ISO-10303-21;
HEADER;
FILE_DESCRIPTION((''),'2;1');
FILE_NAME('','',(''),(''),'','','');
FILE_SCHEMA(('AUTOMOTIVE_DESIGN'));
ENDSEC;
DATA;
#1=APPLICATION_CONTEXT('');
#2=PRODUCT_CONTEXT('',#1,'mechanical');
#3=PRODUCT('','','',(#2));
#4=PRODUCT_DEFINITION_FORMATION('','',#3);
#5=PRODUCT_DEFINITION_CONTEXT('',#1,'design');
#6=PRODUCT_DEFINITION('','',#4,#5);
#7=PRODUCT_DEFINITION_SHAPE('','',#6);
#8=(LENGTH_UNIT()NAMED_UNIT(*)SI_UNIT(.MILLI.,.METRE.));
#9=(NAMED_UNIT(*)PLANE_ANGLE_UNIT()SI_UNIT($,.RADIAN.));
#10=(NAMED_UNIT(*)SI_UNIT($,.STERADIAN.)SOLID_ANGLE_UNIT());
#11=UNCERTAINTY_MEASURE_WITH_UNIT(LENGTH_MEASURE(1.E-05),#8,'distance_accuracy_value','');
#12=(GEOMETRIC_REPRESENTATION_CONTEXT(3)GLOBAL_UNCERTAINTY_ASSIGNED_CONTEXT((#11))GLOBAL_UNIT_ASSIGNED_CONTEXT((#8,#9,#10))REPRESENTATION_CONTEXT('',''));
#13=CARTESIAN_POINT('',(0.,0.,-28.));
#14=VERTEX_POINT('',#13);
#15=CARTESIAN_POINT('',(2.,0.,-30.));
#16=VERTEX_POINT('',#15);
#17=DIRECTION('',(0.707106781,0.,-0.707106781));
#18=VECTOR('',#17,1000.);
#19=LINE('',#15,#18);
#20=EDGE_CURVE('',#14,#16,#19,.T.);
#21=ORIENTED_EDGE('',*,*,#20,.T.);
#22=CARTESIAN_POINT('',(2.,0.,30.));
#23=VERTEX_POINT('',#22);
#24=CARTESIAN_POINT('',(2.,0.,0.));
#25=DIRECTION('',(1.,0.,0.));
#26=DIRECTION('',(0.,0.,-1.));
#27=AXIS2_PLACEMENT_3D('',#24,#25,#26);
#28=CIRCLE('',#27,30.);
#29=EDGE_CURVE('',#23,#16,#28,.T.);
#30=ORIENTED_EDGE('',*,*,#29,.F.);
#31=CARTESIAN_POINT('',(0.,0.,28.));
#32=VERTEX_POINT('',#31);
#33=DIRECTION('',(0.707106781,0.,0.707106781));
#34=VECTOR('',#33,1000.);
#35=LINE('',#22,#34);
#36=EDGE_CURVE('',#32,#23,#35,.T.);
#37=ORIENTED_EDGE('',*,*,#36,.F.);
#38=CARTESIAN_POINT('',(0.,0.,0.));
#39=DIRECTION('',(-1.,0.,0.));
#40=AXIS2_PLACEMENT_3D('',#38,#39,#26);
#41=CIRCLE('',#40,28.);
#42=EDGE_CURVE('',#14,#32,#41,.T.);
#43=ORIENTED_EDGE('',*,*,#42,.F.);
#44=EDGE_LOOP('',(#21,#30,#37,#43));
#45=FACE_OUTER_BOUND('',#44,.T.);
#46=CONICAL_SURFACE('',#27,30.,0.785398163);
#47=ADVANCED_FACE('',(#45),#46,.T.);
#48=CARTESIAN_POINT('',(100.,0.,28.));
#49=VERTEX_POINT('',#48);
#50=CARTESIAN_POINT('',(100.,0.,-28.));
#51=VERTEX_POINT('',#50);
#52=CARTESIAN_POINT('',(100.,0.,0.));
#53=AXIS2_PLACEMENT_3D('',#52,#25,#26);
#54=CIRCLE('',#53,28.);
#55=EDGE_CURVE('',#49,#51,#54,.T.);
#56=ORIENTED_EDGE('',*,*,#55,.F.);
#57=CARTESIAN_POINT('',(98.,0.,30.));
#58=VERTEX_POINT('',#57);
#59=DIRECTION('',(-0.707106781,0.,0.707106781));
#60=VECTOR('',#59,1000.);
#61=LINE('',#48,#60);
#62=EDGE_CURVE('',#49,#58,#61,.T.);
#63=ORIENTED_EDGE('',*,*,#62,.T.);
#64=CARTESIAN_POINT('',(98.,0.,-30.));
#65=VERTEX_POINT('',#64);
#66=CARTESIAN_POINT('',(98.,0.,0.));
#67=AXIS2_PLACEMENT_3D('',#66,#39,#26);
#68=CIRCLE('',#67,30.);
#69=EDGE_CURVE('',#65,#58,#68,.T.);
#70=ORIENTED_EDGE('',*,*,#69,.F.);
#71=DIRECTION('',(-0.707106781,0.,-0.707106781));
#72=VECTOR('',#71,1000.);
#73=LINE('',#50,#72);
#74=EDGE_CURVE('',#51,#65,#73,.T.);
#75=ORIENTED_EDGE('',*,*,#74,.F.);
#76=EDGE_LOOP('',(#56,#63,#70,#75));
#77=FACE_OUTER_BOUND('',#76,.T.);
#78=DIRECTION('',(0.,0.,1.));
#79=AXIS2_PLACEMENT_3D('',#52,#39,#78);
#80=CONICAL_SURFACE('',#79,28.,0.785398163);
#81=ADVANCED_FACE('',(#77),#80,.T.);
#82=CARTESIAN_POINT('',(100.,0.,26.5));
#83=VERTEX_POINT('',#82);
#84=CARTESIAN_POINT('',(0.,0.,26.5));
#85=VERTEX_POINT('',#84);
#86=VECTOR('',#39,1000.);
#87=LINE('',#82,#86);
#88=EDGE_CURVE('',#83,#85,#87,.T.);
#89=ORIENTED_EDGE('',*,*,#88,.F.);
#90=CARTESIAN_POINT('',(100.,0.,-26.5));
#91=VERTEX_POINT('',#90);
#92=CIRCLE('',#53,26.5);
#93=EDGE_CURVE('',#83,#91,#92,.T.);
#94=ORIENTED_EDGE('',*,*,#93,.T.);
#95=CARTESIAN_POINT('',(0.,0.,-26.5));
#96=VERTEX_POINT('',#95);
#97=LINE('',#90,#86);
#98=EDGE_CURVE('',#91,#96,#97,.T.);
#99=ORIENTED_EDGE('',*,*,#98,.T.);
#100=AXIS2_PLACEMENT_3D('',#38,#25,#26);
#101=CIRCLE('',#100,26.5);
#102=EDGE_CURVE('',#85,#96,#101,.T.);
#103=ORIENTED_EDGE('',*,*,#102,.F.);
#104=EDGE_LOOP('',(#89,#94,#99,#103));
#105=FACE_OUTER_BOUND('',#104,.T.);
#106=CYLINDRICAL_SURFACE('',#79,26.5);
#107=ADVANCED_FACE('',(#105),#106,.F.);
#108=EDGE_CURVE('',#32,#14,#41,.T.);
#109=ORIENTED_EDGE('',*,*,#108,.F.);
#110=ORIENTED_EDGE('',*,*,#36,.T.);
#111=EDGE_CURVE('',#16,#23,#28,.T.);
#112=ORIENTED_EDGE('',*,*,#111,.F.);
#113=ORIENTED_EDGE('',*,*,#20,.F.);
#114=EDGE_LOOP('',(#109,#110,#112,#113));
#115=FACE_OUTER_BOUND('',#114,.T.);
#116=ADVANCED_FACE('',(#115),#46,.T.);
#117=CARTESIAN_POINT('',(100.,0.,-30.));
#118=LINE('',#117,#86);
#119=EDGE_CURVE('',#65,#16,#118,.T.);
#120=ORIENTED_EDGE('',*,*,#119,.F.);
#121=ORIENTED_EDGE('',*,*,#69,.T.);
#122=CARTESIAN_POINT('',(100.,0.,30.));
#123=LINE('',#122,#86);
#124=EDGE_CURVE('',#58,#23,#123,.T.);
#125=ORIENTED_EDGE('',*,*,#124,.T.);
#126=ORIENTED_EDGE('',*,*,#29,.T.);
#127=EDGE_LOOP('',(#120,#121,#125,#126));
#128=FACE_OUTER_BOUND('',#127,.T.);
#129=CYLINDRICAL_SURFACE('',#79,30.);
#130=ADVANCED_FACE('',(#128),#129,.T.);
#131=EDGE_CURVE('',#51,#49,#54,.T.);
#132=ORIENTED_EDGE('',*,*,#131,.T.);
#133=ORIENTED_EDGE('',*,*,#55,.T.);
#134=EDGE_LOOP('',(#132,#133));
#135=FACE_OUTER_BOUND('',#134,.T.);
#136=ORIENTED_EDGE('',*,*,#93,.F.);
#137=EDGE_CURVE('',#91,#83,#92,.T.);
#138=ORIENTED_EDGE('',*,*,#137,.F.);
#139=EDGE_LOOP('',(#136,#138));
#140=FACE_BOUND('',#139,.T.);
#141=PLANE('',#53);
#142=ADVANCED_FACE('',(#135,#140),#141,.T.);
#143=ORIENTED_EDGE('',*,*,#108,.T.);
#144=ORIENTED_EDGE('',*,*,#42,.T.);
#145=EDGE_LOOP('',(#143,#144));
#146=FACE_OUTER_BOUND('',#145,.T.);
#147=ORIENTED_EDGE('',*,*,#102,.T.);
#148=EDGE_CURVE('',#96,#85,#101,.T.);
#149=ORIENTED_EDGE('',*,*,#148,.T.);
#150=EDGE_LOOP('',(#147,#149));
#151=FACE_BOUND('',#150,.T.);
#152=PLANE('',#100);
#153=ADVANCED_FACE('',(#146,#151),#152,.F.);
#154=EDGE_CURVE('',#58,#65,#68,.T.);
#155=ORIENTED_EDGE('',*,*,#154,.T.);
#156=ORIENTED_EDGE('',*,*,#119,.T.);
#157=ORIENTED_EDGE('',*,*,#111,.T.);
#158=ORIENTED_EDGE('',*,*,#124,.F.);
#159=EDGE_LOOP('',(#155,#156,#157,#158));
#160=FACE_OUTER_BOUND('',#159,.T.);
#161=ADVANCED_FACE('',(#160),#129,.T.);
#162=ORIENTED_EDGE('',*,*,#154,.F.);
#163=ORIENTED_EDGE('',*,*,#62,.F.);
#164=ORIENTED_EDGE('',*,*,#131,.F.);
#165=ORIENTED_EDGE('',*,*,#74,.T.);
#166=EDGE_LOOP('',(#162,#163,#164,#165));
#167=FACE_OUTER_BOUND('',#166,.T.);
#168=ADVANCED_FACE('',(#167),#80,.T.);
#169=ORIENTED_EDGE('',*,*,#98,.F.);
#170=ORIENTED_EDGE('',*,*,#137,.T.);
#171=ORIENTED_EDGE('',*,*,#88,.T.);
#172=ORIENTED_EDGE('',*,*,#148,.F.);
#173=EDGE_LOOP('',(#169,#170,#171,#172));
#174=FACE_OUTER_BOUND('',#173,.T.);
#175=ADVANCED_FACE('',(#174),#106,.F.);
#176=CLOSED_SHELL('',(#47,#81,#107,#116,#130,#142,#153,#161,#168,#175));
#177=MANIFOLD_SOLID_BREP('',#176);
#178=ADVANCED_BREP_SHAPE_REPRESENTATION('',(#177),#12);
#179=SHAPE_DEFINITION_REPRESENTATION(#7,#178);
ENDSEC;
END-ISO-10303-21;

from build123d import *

# Parameters (mm, degrees)
SKETCH_1_R      = 30
SKETCH_1_R_2    = 26.5
EXTRUDE_1_DEPTH = 100
CHAMFER_1_SIZE  = 2


with BuildPart() as part:
    # 草图1 → 拉伸-薄壁1 (new body)
    with BuildSketch(Plane(origin=(0, 0, 0), x_dir=(0, 0, -1), z_dir=(1, 0, 0))):
        Circle(SKETCH_1_R)
        Circle(SKETCH_1_R_2, mode=Mode.SUBTRACT)
    extrude(amount=EXTRUDE_1_DEPTH)

    # 倒角1
    chamfer_1_edges = [part.edges().sort_by_distance(p)[0] for p in [
        (0, 0, 30),
        (100, 0, 30),
    ]]
    chamfer(chamfer_1_edges, length=CHAMFER_1_SIZE)


solid = part.part
